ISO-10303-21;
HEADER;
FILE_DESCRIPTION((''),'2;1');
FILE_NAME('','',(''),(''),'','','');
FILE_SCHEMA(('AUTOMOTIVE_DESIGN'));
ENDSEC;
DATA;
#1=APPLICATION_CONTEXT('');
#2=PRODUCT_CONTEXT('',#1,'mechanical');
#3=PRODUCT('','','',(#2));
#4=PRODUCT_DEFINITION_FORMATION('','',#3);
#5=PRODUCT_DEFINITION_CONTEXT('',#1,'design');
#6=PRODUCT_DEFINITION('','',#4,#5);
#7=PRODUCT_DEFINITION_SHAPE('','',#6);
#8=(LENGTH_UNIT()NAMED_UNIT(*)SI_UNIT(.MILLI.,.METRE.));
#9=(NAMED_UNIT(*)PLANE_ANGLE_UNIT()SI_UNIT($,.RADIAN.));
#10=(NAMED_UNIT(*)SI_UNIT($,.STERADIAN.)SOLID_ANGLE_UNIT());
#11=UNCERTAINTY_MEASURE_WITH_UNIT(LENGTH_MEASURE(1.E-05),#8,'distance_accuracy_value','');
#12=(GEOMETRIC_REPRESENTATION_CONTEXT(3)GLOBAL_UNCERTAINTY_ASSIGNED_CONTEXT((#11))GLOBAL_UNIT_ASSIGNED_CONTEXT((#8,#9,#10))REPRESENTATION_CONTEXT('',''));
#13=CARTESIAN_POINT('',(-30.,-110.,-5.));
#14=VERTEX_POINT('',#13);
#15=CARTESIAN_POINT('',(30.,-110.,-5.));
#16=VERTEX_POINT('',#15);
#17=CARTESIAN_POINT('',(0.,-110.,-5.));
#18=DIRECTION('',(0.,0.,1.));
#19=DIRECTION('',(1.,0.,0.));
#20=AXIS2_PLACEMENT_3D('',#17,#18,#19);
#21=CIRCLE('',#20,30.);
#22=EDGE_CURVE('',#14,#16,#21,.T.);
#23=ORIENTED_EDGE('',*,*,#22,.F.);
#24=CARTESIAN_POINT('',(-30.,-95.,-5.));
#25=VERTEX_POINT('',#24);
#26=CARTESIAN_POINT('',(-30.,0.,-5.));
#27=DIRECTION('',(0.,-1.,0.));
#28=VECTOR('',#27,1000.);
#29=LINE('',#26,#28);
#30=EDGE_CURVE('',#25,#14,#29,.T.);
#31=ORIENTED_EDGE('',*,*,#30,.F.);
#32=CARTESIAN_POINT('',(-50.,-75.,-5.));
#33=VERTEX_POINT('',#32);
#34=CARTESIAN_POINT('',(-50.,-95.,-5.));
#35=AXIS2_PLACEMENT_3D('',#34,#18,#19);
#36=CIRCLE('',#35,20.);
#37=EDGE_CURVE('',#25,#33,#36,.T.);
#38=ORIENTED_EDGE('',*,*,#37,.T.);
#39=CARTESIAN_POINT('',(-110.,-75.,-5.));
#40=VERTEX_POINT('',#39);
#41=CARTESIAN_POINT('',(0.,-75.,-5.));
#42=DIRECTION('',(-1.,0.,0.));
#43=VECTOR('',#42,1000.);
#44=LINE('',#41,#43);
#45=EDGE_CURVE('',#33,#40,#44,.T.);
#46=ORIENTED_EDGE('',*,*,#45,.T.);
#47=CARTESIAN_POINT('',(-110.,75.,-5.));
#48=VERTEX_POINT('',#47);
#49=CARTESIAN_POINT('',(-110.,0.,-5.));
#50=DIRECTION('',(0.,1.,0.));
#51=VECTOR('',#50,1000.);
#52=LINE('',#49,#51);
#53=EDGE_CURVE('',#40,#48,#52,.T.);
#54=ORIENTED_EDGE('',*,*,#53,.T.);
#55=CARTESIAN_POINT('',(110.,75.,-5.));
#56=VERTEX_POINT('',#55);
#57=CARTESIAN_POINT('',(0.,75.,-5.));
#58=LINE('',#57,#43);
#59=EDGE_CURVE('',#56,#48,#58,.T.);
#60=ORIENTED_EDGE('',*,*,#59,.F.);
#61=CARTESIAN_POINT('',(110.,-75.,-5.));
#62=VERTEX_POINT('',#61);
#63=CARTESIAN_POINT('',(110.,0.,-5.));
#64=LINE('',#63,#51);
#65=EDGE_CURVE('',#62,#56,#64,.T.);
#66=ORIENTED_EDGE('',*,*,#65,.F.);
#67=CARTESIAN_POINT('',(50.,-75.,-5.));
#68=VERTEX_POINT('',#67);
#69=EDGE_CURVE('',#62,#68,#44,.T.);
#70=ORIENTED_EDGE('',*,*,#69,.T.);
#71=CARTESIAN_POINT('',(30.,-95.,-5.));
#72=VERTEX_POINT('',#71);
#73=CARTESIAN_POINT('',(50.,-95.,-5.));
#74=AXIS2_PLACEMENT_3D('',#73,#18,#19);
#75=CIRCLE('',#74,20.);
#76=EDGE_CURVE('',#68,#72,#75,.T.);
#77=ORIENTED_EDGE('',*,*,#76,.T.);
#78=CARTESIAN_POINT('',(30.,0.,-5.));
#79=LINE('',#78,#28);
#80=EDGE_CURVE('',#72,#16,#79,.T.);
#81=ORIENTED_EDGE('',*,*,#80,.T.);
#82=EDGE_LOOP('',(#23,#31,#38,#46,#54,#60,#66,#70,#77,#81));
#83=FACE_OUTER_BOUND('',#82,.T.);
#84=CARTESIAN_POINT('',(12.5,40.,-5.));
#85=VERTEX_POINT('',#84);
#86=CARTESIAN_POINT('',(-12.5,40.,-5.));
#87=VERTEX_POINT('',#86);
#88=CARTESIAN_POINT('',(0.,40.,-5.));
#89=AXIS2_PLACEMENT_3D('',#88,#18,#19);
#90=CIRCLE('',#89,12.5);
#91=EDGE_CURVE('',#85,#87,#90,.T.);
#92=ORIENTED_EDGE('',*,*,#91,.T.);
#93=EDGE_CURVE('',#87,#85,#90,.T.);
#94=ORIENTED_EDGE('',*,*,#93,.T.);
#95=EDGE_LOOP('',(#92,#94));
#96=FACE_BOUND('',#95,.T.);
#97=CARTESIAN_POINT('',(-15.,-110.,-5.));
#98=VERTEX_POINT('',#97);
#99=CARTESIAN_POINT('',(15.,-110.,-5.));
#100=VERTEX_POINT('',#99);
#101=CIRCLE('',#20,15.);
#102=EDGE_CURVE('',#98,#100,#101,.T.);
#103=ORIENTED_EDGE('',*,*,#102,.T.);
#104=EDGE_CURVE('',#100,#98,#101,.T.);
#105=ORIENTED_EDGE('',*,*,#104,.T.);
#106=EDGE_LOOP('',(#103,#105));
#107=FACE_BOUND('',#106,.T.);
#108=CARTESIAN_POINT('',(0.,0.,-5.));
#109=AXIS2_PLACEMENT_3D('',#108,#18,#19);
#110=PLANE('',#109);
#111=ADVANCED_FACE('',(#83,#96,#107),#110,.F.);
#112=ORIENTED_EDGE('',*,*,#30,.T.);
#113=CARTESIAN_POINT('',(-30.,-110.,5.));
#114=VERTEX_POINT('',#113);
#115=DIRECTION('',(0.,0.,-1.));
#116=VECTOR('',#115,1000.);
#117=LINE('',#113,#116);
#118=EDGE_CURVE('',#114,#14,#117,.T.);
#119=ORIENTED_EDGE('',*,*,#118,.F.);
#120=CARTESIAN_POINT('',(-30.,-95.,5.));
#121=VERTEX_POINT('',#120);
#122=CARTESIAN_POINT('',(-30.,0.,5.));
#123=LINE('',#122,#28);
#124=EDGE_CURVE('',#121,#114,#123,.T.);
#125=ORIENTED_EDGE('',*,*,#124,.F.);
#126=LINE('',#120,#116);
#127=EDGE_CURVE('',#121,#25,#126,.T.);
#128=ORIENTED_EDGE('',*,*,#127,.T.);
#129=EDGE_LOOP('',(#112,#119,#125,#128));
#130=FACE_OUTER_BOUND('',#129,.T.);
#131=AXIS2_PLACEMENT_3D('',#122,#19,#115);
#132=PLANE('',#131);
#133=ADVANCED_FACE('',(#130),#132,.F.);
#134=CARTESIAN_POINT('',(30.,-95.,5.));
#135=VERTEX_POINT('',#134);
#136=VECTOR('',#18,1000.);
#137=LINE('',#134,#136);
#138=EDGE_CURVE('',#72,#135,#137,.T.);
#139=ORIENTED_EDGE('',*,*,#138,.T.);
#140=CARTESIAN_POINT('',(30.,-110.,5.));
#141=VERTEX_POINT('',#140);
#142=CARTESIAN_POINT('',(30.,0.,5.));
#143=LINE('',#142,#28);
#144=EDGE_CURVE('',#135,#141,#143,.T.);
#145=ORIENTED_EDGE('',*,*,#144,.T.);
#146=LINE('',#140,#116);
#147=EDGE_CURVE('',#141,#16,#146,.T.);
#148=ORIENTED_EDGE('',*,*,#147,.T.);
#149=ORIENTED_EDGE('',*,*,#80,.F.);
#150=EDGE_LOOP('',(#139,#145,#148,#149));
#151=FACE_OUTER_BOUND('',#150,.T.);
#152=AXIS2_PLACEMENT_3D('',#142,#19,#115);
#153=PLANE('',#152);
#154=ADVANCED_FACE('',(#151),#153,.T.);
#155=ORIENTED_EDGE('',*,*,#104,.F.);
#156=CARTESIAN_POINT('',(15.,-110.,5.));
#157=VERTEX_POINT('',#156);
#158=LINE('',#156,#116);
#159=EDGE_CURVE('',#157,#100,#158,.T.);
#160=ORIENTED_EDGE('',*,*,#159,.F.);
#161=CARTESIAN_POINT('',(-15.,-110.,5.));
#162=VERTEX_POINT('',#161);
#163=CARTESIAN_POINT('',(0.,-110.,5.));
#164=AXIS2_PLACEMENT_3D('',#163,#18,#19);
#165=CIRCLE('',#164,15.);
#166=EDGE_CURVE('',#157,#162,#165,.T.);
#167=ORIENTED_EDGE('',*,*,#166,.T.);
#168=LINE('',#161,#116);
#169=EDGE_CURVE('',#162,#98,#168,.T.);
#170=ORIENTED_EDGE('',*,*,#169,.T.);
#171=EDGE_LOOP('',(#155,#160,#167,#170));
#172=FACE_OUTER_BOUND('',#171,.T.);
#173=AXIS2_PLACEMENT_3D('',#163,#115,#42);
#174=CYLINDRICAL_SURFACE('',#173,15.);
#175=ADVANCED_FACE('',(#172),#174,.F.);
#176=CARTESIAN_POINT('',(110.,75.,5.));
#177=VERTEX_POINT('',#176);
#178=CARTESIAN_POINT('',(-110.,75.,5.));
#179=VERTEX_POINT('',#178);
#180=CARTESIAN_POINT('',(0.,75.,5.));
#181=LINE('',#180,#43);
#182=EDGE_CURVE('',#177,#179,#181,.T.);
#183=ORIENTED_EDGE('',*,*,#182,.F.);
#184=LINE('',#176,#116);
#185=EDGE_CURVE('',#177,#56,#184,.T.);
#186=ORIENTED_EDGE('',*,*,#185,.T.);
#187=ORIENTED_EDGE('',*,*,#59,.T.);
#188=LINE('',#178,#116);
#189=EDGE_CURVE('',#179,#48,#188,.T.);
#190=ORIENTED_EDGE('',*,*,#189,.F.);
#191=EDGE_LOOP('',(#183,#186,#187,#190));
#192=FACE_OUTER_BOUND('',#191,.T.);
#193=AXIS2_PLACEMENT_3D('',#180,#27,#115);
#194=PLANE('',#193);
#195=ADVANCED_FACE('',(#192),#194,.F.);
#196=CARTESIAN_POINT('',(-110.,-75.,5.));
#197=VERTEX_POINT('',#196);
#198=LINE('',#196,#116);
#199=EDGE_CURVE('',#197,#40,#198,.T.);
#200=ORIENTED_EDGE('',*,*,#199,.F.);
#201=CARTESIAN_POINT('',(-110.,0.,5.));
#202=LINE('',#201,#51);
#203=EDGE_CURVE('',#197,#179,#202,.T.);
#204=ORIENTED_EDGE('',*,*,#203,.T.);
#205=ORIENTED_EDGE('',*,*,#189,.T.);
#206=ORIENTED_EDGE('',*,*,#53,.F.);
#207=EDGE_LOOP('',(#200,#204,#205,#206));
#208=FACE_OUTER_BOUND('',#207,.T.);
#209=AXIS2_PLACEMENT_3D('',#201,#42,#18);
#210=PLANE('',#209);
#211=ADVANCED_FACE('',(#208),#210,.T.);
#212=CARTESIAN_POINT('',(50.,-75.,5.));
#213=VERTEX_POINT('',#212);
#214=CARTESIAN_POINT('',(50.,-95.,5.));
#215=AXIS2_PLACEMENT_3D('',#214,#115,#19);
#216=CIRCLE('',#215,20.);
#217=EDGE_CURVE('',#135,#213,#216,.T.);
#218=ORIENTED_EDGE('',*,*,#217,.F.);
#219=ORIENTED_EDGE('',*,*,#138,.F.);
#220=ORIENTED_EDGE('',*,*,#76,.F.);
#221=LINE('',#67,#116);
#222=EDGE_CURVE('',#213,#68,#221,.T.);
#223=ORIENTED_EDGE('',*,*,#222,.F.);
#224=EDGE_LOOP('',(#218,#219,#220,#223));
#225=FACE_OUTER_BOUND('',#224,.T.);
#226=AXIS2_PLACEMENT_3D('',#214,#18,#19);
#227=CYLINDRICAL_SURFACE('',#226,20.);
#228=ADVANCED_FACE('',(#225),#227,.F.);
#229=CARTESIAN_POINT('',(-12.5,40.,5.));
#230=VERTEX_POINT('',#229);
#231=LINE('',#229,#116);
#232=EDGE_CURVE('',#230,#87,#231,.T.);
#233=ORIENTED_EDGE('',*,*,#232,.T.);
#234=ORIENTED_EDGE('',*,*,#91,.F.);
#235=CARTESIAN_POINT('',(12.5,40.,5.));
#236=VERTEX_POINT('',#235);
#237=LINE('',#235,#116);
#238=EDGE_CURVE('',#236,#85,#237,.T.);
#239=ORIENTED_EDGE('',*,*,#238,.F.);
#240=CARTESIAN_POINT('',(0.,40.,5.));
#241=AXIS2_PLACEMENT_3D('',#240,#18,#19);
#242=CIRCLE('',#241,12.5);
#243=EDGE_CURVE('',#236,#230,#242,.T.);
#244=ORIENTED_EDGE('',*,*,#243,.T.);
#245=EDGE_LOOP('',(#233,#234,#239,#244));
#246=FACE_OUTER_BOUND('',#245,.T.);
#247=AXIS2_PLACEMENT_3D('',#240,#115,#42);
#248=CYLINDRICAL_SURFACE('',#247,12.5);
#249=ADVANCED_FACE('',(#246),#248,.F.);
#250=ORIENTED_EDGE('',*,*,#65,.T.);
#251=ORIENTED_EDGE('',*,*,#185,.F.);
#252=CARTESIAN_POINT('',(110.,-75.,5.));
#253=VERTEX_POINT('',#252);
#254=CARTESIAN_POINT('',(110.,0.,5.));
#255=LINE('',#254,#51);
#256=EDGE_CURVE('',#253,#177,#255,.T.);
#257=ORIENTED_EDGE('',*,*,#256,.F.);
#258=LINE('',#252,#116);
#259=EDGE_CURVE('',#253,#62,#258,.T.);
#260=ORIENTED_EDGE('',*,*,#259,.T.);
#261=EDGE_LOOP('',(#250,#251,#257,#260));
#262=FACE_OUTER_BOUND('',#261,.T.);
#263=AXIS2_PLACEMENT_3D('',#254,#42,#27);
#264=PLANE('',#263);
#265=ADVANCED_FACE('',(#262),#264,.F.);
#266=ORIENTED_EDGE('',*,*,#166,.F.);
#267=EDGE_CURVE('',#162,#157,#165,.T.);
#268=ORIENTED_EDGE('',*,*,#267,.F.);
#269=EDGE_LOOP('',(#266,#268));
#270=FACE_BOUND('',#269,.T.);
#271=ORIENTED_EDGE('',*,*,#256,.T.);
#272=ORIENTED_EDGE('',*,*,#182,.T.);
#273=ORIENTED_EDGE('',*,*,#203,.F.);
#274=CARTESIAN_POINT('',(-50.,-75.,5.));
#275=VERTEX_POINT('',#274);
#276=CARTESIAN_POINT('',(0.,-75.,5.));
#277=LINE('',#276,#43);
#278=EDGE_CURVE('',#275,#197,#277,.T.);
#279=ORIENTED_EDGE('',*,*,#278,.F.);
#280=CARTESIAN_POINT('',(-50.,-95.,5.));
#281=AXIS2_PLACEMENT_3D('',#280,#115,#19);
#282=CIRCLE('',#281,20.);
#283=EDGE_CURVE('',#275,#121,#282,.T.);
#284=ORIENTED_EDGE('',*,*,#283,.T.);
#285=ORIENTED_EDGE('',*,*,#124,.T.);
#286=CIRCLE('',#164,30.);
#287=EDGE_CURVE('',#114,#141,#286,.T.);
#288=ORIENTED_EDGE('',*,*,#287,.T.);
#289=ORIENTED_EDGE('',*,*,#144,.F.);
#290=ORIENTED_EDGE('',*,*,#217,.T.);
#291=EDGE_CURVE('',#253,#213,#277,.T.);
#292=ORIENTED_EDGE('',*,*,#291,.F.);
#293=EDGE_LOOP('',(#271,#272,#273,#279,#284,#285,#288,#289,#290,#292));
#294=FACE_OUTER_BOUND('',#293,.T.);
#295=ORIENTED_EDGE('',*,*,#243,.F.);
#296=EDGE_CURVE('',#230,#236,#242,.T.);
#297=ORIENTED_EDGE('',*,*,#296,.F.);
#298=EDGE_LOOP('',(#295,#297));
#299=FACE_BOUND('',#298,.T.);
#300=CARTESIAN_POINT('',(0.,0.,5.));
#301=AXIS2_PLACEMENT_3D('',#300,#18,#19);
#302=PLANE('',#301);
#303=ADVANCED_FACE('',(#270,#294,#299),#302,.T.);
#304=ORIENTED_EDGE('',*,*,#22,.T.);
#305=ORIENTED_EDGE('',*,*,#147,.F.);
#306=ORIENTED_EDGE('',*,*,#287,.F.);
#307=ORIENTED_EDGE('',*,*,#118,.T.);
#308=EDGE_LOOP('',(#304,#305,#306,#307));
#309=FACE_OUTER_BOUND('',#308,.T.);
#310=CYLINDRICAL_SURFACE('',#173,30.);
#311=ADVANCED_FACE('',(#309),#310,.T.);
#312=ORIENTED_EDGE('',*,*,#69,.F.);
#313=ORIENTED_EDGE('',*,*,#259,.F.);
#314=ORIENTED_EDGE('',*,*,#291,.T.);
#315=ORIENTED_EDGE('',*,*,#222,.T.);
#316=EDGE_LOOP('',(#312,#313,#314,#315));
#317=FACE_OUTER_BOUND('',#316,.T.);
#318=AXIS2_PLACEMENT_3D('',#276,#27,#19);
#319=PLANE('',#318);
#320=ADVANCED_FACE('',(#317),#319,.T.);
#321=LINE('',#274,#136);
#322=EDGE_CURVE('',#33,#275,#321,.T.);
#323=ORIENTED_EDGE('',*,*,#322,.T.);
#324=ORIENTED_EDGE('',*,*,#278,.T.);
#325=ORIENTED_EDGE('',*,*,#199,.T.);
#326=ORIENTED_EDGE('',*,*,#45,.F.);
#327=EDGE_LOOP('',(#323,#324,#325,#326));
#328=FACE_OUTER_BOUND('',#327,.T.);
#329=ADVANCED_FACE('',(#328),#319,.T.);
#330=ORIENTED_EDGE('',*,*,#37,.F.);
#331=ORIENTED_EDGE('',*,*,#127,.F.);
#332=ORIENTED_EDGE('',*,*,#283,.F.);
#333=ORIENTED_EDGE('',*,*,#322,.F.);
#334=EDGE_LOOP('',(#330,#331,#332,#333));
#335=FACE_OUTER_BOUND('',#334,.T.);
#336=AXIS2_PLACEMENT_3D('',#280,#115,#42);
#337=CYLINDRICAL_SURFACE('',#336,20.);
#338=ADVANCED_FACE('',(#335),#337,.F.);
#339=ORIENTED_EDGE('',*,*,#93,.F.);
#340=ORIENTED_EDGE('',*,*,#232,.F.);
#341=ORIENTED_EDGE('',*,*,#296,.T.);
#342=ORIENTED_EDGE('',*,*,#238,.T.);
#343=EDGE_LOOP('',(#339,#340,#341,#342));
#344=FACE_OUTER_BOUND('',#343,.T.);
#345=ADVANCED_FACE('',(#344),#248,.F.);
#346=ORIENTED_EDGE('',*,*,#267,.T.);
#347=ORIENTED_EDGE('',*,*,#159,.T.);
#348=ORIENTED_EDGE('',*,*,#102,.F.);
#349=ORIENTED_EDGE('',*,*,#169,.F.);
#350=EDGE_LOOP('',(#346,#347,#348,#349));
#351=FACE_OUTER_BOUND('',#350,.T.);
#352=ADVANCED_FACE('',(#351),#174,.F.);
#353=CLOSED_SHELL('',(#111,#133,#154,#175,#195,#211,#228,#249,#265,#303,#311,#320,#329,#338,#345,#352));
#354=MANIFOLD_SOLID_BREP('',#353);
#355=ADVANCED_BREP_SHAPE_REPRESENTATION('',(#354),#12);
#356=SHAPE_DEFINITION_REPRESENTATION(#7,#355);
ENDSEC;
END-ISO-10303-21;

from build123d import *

# Parameters (mm, degrees)
SKETCH1_R           = 15
SKETCH1_R_2         = 12.5
BOSS_EXTRUDE1_DEPTH = 5
FILLET1_R           = 20


with BuildPart() as part:
    # Sketch1 → Boss-Extrude1 (new, symmetric)
    # profile 1 of 3: a face of its own
    with BuildSketch(Plane.XY):
        with BuildLine():
            Line((30, -110), (30, -75))
            Line((30, -75), (-30, -75))
            Line((-30, -75), (-30, -110))
            ThreePointArc((-30, -110), (0, -140), (30, -110))
        make_face()
        with Locations((0, -110)):
            Circle(SKETCH1_R, mode=Mode.SUBTRACT)
    # profile 2 of 3: a face of its own
    with BuildSketch(Plane.XY):
        with BuildLine():
            Line((30, -75), (110, -75))
            Line((110, -75), (110, 75))
            Line((110, 75), (-110, 75))
            Line((-110, 75), (-110, -75))
            Line((-110, -75), (-30, -75))
            ThreePointArc((-30, -75), (0, -45), (30, -75))
        make_face()
        with Locations((0, 40)):
            Circle(SKETCH1_R_2, mode=Mode.SUBTRACT)
    # profile 3 of 3: a face of its own
    with BuildSketch(Plane.XY):
        with BuildLine():
            Line((-30, -75), (30, -75))
            ThreePointArc((30, -75), (0, -45), (-30, -75))
        make_face()
    extrude(amount=BOSS_EXTRUDE1_DEPTH, both=True)

    # Fillet1
    fillet1_edges = [part.edges().sort_by_distance(p)[0] for p in [
        (-30, -75, 0),
        (30, -75, 0),
    ]]
    fillet(fillet1_edges, radius=FILLET1_R)


solid = part.part
